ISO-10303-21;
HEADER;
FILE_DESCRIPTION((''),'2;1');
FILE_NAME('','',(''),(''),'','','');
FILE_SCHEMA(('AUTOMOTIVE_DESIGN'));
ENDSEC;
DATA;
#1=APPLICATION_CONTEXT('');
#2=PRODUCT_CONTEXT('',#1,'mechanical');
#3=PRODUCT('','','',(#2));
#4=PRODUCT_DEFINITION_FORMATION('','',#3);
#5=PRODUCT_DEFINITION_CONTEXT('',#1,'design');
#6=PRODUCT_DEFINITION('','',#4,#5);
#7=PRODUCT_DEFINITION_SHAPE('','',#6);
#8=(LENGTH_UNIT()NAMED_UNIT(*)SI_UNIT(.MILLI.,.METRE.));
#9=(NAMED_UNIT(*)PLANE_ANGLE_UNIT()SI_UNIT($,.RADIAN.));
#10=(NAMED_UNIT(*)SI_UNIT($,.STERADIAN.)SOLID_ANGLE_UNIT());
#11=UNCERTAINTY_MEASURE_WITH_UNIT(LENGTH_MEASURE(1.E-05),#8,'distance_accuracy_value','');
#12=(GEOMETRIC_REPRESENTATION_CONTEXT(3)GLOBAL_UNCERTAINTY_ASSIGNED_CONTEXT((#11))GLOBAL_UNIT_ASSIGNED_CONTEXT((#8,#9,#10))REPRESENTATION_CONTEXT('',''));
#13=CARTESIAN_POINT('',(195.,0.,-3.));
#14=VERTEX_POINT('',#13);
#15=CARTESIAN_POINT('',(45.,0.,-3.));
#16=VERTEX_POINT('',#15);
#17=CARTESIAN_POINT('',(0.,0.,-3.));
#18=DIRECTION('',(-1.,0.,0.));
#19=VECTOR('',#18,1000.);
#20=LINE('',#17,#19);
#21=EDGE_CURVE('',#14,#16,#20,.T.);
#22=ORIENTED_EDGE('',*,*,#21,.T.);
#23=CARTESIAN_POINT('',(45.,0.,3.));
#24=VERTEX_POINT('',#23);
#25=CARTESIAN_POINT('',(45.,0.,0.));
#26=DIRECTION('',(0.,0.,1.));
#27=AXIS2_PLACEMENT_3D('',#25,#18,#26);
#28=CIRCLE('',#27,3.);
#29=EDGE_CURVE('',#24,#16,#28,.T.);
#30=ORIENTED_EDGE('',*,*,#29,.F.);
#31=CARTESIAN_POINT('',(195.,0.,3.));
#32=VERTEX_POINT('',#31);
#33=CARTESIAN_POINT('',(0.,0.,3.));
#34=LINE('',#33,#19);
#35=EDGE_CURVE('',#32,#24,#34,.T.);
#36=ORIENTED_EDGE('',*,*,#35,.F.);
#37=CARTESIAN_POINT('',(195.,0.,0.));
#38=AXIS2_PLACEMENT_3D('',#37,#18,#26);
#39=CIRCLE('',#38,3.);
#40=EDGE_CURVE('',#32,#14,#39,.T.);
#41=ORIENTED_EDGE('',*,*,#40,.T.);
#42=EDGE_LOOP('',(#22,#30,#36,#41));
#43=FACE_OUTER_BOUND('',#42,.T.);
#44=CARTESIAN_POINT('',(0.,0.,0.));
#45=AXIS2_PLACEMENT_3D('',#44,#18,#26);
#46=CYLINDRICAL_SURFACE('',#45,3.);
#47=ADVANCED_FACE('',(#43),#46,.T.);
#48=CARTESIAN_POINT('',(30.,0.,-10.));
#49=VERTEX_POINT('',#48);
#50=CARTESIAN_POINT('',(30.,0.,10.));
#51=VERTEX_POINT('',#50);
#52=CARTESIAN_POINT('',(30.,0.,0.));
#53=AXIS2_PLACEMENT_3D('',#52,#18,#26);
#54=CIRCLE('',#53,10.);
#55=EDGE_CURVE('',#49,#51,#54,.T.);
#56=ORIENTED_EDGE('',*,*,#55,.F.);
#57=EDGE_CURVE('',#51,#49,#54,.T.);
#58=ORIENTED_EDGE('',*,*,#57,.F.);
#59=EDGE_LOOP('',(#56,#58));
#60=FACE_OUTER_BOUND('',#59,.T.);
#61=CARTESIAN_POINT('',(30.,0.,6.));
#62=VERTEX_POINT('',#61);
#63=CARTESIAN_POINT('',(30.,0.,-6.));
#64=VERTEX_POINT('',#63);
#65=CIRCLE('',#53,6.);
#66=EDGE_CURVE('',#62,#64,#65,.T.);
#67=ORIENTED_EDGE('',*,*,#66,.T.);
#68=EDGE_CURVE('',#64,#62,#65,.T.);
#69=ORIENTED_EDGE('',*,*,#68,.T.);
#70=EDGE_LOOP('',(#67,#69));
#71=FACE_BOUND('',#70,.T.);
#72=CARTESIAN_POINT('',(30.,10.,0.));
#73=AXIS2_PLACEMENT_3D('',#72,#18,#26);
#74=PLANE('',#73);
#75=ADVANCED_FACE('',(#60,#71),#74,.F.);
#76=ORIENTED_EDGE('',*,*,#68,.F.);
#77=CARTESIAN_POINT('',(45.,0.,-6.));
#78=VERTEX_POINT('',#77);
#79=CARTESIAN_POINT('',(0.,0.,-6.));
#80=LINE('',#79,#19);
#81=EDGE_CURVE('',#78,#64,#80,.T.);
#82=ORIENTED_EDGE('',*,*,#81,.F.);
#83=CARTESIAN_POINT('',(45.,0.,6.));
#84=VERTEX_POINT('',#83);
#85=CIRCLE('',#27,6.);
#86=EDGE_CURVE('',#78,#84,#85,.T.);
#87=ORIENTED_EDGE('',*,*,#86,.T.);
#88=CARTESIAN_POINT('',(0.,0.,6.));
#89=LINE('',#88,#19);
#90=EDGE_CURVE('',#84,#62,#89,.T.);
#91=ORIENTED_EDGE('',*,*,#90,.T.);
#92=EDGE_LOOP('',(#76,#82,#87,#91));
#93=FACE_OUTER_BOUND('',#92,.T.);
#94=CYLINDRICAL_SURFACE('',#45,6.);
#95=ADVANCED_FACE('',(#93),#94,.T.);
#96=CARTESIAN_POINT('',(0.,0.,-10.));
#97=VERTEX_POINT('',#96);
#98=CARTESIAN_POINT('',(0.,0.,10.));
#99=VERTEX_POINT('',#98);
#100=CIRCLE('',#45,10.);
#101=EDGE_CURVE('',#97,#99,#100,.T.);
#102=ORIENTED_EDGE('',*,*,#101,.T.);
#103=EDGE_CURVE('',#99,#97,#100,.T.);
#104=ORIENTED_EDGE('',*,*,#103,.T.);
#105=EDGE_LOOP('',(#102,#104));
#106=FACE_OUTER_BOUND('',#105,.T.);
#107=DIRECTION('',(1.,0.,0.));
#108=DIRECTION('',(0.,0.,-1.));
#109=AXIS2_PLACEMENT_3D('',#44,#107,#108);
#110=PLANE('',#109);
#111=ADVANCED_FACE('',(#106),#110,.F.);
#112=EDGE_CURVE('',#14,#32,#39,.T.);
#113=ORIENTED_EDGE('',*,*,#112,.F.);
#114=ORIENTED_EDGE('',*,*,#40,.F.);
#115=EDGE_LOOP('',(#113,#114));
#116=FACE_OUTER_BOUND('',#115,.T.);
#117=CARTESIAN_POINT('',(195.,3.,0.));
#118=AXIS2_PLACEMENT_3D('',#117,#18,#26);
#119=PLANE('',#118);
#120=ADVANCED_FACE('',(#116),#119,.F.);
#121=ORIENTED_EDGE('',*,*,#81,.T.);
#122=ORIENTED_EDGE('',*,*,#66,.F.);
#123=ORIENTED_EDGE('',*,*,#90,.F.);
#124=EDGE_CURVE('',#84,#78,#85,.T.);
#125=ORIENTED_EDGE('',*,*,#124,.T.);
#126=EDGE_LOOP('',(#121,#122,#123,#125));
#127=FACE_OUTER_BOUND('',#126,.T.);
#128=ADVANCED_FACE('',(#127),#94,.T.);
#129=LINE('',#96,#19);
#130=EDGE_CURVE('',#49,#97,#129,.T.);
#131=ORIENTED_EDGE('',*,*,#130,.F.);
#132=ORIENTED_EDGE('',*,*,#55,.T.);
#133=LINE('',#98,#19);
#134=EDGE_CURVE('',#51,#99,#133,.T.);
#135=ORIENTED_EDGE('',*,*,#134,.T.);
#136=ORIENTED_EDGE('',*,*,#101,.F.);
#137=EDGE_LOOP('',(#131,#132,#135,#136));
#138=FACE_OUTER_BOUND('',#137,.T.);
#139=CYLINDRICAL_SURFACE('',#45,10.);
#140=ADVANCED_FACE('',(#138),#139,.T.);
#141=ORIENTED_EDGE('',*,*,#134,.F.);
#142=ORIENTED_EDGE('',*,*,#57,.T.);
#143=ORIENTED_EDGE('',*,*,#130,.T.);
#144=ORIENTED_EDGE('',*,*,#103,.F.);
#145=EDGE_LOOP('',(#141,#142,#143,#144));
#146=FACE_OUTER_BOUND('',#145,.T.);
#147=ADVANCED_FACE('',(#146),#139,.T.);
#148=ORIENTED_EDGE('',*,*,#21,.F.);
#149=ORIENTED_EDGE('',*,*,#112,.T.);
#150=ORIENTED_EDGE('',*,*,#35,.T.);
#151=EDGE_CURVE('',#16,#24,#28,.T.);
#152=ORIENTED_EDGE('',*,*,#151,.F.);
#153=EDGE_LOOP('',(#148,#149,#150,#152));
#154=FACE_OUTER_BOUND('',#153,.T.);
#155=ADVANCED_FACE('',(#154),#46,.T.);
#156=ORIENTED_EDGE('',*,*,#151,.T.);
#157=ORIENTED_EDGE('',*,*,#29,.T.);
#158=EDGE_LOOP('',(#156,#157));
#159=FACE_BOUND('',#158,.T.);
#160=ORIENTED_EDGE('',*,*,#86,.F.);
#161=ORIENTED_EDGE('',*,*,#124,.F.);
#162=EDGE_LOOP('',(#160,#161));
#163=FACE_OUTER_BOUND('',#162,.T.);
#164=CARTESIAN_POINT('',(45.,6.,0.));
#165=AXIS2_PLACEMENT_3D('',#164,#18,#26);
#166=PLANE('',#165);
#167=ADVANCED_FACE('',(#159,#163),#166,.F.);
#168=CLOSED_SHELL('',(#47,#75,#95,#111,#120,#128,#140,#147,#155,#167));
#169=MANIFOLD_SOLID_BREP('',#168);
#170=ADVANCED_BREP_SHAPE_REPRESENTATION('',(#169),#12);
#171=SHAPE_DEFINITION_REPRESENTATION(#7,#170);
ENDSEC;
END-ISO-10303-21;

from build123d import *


with BuildPart() as part:
    # Sketch1 → Revolve1 (revolve)
    with BuildSketch(Plane.XY, mode=Mode.PRIVATE) as revolve1_sk:
        Polygon((0, 0), (0, 10), (30, 10), (30, 6), (45, 6), (45, 3), (195, 3), (195, 0), align=None)
    revolve(revolve1_sk.sketch.rotate(Axis((0, 0, 0), (1, 0, 0)), 90), axis=Axis((0, 0, 0), (1, 0, 0)))


solid = part.part
